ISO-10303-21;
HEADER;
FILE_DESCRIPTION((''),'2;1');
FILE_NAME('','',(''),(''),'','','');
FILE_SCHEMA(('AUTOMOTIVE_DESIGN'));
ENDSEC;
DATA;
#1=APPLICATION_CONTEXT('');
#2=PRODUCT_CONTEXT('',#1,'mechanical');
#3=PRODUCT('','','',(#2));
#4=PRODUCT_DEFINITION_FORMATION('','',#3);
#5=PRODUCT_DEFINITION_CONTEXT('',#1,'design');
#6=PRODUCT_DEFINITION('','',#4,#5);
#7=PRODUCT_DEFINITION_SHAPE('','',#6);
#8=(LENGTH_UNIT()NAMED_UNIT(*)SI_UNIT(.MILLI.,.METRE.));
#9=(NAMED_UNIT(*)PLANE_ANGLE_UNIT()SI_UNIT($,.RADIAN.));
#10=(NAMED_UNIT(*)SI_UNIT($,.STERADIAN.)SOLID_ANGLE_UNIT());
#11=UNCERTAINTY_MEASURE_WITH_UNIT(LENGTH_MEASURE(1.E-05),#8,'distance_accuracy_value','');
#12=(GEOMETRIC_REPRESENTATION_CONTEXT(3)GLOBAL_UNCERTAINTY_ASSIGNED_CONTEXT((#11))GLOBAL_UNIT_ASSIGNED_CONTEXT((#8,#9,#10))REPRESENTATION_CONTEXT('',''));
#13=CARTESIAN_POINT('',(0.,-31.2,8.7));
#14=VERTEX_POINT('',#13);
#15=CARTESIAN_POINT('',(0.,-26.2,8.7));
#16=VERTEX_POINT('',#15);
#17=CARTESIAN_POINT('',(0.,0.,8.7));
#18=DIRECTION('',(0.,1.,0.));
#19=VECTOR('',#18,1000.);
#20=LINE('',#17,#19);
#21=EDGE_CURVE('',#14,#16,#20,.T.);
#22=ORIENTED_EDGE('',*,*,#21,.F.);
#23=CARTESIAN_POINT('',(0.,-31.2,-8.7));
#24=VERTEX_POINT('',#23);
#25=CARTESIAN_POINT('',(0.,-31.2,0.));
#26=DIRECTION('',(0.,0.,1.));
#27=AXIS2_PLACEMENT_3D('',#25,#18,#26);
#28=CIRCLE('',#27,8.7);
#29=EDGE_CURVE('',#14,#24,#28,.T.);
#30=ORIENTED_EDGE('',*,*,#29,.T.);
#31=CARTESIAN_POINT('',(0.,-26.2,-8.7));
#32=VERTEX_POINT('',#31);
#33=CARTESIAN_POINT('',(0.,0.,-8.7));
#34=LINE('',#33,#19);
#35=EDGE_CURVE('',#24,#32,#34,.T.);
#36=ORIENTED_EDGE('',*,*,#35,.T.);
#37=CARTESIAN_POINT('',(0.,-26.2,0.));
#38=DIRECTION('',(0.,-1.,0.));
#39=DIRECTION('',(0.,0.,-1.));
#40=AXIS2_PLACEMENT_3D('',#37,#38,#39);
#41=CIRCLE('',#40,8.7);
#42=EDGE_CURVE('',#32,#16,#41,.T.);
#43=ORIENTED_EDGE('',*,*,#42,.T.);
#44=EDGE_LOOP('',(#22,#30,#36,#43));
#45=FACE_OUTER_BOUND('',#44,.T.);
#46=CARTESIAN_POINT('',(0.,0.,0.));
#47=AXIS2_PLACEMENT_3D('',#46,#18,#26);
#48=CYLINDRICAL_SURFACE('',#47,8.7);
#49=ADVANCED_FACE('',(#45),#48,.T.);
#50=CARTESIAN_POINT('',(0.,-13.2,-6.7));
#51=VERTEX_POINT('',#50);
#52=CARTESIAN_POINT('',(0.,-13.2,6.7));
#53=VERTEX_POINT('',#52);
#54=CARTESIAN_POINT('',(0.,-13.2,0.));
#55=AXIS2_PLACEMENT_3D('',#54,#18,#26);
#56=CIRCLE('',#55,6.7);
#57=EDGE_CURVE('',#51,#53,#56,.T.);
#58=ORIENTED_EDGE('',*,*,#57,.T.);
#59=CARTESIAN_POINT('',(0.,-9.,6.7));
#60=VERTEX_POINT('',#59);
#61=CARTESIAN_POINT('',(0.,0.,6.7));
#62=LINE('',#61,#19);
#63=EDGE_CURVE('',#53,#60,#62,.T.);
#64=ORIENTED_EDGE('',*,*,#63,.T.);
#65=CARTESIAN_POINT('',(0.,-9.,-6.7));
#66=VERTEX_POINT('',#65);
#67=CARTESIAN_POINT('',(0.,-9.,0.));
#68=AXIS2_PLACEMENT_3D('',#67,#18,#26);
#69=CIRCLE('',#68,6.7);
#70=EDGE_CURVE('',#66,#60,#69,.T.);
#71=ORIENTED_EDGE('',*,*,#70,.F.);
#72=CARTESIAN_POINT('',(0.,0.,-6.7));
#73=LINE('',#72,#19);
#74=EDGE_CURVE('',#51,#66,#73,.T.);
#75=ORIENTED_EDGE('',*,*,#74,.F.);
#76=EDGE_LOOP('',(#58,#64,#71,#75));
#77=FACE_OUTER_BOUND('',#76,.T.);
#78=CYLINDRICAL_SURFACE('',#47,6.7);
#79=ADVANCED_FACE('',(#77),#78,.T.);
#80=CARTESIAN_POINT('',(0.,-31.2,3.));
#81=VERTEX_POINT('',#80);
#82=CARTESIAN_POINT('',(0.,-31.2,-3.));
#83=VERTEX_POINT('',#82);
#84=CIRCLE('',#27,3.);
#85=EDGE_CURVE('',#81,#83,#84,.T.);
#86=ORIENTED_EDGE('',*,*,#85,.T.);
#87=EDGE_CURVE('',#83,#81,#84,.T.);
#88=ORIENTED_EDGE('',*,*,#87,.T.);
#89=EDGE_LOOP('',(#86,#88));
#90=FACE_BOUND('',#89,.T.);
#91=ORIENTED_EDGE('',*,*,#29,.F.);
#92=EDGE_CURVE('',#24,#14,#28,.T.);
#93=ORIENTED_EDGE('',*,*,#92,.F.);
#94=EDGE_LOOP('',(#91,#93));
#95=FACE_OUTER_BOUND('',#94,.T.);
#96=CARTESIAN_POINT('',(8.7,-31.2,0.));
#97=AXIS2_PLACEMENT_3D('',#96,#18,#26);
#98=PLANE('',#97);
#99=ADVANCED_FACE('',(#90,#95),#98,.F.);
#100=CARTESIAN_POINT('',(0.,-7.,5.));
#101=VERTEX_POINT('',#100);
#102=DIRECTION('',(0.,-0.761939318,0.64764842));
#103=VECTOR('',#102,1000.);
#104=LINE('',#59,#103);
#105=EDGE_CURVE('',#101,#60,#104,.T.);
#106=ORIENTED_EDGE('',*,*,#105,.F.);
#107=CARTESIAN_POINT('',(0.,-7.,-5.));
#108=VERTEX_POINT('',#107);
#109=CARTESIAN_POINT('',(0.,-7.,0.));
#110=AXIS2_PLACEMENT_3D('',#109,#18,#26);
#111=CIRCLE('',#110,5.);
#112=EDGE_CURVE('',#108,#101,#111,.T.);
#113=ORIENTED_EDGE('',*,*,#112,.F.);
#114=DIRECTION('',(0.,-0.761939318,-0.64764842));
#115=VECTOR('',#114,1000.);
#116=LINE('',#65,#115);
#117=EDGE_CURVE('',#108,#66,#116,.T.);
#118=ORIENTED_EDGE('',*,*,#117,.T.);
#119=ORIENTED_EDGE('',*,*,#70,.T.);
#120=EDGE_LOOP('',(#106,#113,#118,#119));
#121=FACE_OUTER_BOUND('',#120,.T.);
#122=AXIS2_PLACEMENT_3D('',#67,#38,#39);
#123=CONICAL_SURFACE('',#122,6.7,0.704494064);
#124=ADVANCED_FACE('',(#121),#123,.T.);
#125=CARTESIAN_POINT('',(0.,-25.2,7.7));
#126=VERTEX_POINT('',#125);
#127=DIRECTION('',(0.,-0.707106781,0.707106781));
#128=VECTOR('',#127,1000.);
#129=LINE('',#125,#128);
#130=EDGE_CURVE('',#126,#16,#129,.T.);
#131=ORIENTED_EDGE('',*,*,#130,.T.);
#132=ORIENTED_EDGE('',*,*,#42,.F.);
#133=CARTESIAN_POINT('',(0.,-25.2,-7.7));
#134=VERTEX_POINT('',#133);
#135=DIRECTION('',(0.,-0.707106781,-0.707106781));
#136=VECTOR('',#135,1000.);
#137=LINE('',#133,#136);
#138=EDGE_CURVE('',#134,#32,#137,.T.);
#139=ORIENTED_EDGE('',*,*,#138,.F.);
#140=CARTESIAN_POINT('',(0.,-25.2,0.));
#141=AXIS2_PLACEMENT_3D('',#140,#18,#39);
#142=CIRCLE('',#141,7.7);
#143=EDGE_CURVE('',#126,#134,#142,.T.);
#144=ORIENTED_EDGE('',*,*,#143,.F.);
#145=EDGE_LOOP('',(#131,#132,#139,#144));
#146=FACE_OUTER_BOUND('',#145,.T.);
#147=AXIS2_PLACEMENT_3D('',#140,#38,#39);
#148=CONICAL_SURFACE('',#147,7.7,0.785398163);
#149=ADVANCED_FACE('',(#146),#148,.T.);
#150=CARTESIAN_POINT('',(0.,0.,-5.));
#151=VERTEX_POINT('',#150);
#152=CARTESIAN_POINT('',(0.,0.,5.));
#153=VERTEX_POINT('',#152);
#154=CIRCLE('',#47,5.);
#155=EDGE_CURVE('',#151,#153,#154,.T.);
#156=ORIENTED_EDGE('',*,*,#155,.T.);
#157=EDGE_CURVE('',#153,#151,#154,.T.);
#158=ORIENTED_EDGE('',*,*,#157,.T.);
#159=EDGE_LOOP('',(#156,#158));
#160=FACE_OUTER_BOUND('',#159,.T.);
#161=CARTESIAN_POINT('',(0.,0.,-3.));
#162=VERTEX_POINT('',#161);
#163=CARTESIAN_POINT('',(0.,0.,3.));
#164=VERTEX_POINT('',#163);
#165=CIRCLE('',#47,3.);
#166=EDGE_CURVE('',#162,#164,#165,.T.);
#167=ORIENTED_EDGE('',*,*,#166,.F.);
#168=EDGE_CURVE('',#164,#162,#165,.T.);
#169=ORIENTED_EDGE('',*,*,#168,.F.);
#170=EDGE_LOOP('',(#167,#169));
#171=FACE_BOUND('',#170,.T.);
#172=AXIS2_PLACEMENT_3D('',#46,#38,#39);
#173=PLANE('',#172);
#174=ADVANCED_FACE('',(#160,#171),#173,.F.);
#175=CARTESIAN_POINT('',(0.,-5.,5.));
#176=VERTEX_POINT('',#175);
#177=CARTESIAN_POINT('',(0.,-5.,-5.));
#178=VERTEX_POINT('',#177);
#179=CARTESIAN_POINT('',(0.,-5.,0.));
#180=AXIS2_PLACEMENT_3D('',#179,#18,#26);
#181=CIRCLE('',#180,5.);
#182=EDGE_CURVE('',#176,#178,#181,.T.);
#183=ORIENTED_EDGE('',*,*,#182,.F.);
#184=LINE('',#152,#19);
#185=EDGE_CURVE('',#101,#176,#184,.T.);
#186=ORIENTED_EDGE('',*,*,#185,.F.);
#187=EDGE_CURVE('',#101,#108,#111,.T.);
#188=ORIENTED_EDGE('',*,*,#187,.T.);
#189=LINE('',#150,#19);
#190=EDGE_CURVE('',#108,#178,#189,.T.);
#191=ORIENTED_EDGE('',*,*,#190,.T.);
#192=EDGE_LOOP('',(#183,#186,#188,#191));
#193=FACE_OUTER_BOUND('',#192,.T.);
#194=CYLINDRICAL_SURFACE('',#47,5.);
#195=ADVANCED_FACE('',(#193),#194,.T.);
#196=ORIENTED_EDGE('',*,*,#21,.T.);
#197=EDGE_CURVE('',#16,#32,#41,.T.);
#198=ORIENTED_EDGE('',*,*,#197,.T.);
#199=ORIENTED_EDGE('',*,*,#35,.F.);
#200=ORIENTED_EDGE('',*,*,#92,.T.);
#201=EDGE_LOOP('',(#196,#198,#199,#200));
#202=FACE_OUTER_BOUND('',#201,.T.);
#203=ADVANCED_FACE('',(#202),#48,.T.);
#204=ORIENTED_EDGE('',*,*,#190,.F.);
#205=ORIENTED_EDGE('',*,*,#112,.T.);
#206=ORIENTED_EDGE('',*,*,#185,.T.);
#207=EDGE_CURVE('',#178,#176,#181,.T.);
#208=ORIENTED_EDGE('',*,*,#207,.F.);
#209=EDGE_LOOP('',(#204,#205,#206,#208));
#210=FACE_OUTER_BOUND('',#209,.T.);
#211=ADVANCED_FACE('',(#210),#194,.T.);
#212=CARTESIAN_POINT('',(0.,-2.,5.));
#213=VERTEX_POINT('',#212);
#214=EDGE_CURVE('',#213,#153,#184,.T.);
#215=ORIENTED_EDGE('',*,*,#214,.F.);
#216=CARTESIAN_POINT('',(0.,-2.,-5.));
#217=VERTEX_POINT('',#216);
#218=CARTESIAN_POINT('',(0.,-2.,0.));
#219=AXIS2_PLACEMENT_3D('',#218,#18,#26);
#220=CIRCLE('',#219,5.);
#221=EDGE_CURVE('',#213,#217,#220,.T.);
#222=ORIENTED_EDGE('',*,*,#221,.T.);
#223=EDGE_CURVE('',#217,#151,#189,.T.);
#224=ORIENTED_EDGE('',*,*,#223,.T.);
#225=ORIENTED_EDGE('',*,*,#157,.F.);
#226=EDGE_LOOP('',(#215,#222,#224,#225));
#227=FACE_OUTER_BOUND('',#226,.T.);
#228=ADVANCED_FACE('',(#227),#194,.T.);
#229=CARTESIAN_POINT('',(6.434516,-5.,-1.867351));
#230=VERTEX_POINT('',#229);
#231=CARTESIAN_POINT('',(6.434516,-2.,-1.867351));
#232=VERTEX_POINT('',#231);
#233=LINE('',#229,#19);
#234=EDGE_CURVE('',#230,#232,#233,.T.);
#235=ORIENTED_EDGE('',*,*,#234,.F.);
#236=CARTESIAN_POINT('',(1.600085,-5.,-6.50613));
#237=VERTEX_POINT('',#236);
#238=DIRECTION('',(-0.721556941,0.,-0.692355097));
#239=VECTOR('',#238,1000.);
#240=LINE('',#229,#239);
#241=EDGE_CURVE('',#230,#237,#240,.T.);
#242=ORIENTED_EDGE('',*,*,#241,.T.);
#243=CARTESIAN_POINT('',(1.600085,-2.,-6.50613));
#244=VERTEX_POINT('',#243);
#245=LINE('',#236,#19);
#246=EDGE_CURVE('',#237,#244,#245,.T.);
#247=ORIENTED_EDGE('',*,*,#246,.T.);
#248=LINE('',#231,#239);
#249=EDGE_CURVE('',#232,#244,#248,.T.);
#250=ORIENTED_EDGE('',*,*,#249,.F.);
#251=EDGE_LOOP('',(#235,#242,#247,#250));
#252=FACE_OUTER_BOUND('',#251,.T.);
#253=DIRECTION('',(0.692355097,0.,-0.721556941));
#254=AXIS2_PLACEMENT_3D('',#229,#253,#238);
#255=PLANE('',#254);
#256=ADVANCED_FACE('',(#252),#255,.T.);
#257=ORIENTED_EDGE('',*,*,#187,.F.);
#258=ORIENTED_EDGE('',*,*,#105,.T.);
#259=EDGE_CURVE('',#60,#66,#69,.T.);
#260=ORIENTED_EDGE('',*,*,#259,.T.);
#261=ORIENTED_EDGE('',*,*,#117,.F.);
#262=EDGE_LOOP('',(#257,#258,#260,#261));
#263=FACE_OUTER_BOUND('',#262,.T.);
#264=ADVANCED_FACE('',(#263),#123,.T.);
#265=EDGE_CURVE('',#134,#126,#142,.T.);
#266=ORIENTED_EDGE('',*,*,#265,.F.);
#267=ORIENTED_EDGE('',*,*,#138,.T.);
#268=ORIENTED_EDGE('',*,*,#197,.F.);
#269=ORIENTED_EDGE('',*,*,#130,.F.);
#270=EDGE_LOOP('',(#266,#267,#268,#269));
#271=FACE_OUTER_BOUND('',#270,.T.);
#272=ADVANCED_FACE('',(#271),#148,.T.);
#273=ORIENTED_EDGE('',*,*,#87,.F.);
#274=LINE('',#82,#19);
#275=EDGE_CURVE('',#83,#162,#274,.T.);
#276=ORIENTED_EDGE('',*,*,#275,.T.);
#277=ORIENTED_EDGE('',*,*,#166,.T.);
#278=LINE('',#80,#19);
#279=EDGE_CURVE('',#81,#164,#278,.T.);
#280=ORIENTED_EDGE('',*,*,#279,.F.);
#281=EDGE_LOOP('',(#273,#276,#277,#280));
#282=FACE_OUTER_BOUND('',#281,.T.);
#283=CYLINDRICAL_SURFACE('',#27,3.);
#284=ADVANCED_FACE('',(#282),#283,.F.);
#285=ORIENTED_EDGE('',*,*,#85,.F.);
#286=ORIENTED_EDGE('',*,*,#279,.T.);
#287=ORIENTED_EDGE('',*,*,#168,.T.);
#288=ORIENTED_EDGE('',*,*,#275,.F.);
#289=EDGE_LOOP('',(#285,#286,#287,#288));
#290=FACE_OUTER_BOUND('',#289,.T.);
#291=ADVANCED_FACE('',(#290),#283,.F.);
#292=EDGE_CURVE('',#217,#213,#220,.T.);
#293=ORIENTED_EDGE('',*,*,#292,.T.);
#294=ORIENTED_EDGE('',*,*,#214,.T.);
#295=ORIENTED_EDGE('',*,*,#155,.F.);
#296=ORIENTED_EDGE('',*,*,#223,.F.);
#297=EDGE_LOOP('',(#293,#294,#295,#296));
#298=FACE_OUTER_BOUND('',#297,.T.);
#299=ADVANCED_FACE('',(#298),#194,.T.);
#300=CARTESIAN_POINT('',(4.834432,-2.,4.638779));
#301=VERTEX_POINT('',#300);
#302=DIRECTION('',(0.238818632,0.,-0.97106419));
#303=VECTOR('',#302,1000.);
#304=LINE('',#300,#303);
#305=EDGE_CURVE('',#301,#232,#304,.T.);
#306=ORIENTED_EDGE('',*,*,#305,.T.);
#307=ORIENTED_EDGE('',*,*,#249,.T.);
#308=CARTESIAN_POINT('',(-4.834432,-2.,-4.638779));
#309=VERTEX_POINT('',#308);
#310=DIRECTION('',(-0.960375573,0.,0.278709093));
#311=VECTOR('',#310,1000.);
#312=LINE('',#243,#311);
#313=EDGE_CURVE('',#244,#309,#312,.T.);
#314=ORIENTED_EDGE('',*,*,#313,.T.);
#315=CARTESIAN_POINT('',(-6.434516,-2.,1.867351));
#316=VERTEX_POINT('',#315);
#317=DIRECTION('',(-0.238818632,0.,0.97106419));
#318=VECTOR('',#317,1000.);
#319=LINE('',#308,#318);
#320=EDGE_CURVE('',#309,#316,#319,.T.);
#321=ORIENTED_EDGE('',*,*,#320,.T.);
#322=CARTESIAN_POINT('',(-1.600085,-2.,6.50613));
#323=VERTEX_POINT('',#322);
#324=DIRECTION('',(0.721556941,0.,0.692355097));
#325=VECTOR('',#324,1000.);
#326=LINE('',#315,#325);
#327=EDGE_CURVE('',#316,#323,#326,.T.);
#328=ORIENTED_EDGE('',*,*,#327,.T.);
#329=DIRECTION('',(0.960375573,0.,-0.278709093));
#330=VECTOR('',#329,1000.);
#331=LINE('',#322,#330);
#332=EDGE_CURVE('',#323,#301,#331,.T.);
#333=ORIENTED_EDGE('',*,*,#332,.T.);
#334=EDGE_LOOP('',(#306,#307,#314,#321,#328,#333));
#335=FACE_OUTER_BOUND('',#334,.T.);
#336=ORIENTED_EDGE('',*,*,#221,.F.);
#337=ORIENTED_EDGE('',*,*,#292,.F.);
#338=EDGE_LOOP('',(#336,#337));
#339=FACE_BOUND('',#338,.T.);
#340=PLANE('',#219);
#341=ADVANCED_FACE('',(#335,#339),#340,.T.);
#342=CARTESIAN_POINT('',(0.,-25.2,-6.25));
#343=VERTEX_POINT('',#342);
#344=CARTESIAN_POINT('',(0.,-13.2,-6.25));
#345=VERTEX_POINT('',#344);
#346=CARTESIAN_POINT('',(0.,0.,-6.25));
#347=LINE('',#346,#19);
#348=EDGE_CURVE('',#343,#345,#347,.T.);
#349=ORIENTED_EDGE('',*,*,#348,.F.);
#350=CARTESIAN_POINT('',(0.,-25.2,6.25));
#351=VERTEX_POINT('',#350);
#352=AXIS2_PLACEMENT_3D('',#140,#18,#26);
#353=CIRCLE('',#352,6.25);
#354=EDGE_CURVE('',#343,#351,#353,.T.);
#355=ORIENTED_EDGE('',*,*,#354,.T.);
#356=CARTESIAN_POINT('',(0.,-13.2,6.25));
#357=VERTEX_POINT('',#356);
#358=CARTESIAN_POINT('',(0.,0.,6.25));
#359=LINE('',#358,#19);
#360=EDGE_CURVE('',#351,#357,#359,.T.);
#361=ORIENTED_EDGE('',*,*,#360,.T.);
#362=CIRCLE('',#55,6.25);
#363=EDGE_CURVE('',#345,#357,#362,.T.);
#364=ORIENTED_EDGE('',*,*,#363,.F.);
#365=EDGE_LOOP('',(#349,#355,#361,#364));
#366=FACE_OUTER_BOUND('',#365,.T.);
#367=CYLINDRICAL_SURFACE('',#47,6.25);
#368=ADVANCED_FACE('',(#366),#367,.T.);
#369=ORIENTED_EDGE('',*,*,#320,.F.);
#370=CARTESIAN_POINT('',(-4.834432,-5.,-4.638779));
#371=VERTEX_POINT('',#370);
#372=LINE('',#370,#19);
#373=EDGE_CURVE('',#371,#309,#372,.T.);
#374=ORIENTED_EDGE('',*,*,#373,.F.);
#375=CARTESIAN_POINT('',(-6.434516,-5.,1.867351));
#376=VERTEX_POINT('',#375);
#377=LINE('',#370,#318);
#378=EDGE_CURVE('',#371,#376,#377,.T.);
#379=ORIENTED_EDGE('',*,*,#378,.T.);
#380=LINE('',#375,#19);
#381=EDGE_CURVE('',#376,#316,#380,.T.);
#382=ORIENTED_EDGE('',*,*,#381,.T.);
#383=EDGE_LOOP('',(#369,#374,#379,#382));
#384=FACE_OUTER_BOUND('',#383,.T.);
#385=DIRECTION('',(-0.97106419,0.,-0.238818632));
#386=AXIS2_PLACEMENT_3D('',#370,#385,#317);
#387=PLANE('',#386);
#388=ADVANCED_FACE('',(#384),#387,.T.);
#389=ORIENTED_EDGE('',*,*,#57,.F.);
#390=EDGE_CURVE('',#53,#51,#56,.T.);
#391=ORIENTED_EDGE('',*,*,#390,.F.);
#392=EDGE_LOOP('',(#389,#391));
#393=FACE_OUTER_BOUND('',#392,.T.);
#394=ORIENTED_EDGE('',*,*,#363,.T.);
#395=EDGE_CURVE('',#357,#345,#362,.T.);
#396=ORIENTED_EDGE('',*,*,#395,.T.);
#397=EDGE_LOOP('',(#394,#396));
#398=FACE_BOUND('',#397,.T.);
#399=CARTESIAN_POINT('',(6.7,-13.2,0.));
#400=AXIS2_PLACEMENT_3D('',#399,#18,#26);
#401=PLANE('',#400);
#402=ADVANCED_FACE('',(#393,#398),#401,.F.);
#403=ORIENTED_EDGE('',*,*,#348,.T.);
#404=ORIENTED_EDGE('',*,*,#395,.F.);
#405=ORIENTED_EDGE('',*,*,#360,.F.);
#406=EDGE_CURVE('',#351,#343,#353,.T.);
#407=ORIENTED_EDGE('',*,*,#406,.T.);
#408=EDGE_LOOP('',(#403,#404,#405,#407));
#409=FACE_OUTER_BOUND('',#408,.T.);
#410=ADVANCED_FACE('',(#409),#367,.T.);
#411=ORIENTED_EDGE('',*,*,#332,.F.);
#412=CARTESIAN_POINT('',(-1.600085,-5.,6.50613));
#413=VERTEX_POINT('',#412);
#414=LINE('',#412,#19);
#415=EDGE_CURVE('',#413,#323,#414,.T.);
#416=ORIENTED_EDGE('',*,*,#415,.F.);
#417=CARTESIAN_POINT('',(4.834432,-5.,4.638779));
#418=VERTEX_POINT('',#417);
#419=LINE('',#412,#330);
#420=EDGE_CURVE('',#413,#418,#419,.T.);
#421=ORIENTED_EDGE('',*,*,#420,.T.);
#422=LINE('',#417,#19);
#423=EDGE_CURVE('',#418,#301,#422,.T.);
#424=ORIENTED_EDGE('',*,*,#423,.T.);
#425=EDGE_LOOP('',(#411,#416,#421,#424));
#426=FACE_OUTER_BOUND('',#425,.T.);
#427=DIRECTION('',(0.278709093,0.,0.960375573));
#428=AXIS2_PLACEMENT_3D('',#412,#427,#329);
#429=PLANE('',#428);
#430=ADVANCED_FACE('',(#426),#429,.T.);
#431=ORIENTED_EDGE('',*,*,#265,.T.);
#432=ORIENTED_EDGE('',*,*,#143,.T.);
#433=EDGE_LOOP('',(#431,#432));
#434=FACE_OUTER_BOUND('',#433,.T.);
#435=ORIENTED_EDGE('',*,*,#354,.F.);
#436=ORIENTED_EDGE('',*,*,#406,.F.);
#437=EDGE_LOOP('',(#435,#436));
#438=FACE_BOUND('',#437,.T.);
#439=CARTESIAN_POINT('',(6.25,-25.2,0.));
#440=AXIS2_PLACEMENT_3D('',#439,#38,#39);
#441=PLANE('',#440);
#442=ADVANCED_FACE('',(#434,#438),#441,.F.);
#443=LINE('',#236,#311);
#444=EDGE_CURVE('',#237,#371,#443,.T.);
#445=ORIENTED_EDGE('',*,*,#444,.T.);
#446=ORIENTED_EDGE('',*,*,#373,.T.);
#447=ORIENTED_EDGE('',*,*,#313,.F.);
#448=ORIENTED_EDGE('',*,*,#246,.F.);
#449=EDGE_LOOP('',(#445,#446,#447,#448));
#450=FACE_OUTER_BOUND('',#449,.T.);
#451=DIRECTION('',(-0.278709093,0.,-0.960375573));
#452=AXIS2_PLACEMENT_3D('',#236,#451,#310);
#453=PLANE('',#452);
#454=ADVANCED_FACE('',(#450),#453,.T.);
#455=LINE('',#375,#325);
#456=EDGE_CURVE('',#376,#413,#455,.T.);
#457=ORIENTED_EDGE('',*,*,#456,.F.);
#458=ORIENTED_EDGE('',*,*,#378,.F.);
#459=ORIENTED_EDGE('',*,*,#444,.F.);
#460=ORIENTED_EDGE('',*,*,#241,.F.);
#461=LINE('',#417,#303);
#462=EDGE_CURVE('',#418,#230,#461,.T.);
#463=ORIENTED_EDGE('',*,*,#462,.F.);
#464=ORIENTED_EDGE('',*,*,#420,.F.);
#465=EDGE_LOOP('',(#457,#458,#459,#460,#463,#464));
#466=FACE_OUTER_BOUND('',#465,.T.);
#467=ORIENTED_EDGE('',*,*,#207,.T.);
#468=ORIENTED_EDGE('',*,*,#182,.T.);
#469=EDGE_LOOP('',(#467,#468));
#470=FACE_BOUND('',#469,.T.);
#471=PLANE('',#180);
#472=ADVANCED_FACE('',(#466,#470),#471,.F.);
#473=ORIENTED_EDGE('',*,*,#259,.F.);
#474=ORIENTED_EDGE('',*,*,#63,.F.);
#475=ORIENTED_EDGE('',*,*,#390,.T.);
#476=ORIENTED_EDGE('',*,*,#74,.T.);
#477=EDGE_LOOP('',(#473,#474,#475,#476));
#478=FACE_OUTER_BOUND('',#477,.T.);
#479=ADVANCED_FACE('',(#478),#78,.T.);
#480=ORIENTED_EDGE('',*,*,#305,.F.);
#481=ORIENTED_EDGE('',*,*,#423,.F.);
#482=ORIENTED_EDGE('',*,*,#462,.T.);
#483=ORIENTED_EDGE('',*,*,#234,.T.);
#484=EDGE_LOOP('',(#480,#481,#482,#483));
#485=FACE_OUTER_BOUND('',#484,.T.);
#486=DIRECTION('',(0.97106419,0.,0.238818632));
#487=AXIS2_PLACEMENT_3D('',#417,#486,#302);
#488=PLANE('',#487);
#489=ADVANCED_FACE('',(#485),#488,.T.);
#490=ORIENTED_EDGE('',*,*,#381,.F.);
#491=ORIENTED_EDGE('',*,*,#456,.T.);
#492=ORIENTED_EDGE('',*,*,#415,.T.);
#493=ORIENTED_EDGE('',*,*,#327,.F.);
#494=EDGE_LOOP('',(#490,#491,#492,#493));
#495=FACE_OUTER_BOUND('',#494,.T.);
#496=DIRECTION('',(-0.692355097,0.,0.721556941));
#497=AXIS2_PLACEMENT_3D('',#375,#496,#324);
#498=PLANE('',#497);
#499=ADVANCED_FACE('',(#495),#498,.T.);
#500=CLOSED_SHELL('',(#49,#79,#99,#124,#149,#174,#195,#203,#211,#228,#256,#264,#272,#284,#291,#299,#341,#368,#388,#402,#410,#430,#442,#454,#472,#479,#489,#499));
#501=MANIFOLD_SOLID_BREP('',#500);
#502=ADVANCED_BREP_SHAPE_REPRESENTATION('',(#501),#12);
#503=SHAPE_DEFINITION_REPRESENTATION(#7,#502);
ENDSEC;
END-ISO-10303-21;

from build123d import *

# Parameters (mm, degrees)
BOSS_EXTRUDE1_DEPTH = 3
SKETCH3_R           = 3
CUT_EXTRUDE1_DEPTH  = 34.538336274
CHAMFER1_SIZE       = 1


with BuildPart() as part:
    # Sketch1 → Revolve1 (revolve)
    with BuildSketch(Plane.XY, mode=Mode.PRIVATE) as revolve1_sk:
        Polygon((0, 0), (5, 0), (5, -7), (6.7, -9), (6.7, -13.2), (6.25, -13.2), (6.25, -25.2), (8.7, -25.2), (8.7, -31.2), (0, -31.2), align=None)
    revolve(revolve1_sk.sketch.rotate(Axis((0, 0, 0), (0, -1, 0)), 90), axis=Axis((0, 0, 0), (0, -1, 0)))

    # Sketch2 → Boss-Extrude1 (add)
    with BuildSketch(Plane(origin=(0, -2, 0), x_dir=(1, 0, 0), z_dir=(0, 1, 0))):
        Polygon((-1.600084835, -6.506130073), (4.834431506, -4.638779152), (6.434516341, 1.867350921), (1.600084835, 6.506130073), (-4.834431506, 4.638779152), (-6.434516341, -1.867350921), align=None)
    extrude(amount=-BOSS_EXTRUDE1_DEPTH)

    # Sketch3 → Cut-Extrude1 (cut, through all)
    with BuildSketch(Plane(origin=(0, 0, 0), x_dir=(1, 0, 0), z_dir=(0, 1, 0))):
        with Locations(Location((0, 0, 0), (0, 0, 270))):
            Circle(SKETCH3_R)
    extrude(amount=-CUT_EXTRUDE1_DEPTH, mode=Mode.SUBTRACT)

    # Chamfer1
    chamfer1_edges = [part.edges().sort_by_distance(p)[0] for p in [
        (0, -25.2, -8.7),
    ]]
    chamfer(chamfer1_edges, length=CHAMFER1_SIZE)


solid = part.part
